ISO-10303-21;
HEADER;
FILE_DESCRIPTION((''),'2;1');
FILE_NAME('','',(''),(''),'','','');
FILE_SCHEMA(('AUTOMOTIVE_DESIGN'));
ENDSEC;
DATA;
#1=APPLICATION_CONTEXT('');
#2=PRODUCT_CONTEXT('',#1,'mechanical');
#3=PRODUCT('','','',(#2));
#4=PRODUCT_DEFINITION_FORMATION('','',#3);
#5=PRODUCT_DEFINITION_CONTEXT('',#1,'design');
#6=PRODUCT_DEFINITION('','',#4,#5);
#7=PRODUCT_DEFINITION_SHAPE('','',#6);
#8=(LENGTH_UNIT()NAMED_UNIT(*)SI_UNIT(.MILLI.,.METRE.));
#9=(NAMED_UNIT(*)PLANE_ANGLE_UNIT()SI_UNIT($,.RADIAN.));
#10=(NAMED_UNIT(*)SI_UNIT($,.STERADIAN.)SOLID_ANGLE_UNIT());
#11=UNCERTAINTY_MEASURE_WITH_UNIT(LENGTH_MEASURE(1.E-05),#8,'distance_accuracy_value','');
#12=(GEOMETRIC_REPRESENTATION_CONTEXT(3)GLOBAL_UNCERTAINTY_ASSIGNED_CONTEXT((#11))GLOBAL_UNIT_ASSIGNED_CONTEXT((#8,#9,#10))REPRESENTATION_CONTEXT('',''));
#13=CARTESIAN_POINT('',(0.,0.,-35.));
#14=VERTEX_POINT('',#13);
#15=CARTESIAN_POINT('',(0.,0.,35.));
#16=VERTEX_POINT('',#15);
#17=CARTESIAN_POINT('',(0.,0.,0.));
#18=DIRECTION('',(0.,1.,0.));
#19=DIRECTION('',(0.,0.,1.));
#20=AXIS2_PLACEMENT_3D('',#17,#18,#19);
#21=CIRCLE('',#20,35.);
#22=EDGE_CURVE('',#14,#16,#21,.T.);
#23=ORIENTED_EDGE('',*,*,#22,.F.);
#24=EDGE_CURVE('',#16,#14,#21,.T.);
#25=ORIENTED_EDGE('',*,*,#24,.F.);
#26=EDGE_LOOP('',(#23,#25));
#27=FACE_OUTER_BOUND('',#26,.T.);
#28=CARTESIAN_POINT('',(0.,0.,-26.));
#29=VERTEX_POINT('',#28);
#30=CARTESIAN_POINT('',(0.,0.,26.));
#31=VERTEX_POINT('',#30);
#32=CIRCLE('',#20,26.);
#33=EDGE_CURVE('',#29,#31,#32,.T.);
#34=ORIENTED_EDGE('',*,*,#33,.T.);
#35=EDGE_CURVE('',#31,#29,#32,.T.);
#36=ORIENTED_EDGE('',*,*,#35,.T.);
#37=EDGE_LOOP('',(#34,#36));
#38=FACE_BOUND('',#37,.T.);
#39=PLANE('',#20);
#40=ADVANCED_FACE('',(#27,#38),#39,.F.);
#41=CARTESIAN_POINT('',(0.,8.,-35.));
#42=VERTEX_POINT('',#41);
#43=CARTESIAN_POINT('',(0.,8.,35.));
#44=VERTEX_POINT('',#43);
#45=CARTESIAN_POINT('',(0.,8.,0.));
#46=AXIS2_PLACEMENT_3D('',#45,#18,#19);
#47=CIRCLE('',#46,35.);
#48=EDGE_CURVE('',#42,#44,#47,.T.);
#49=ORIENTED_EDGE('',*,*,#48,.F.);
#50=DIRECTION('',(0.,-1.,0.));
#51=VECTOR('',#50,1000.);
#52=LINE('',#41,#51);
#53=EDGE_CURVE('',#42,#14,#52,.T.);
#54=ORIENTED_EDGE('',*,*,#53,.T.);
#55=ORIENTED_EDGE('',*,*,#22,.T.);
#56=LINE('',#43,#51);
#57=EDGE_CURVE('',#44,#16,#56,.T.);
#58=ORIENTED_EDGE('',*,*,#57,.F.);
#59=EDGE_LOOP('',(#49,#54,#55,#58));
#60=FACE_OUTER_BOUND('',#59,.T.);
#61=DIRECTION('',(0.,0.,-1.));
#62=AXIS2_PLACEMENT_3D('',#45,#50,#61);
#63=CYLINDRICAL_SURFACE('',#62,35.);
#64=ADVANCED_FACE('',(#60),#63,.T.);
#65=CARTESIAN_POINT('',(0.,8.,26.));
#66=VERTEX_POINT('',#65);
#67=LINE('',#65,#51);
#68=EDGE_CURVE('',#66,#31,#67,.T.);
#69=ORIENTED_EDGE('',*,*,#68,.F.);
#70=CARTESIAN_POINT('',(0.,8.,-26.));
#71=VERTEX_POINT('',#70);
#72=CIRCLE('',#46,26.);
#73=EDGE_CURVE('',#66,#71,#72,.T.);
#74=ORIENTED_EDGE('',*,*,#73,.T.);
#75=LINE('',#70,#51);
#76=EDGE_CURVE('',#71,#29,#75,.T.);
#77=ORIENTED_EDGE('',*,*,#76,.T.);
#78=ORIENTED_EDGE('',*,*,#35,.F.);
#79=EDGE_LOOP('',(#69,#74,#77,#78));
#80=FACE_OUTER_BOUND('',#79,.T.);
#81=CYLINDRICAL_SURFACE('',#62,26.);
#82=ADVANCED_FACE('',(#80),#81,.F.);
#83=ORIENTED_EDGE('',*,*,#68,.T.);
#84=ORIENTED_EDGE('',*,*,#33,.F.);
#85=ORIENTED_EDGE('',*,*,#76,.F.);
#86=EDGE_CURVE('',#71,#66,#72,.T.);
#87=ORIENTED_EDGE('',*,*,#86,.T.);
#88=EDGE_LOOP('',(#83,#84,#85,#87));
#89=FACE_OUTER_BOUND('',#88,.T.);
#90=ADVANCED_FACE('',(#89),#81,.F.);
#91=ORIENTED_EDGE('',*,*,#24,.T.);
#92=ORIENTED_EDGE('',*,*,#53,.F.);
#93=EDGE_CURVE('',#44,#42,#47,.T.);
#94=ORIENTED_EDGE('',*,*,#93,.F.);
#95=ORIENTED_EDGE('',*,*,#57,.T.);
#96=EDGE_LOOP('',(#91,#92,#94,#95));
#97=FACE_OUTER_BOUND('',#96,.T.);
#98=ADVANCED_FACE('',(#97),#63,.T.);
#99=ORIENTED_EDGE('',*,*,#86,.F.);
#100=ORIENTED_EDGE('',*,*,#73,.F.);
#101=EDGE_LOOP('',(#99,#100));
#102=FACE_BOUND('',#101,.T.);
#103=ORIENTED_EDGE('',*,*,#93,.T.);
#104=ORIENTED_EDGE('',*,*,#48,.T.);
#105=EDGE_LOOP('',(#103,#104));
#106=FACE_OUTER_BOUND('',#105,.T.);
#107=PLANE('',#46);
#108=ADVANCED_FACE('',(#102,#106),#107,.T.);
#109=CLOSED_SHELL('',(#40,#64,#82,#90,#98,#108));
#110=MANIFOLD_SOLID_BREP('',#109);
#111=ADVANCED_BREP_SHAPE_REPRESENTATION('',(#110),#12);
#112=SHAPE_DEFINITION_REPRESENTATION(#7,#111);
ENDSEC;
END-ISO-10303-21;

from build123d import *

# Parameters (mm, degrees)
SKETCH_1_R           = 35
SKETCH_1_R_2         = 26
BOSS_EXTRUDE_1_DEPTH = 8


with BuildPart() as part:
    # Sketch 1 → Boss-Extrude 1 (new body)
    with BuildSketch(Plane(origin=(0, 0, 0), x_dir=(1, 0, 0), z_dir=(0, 1, 0))):
        with Locations(Location((0, 0, 0), (0, 0, 270))):
            Circle(SKETCH_1_R)
        with Locations(Location((0, 0, 0), (0, 0, 270))):
            Circle(SKETCH_1_R_2, mode=Mode.SUBTRACT)
    extrude(amount=BOSS_EXTRUDE_1_DEPTH)


solid = part.part
